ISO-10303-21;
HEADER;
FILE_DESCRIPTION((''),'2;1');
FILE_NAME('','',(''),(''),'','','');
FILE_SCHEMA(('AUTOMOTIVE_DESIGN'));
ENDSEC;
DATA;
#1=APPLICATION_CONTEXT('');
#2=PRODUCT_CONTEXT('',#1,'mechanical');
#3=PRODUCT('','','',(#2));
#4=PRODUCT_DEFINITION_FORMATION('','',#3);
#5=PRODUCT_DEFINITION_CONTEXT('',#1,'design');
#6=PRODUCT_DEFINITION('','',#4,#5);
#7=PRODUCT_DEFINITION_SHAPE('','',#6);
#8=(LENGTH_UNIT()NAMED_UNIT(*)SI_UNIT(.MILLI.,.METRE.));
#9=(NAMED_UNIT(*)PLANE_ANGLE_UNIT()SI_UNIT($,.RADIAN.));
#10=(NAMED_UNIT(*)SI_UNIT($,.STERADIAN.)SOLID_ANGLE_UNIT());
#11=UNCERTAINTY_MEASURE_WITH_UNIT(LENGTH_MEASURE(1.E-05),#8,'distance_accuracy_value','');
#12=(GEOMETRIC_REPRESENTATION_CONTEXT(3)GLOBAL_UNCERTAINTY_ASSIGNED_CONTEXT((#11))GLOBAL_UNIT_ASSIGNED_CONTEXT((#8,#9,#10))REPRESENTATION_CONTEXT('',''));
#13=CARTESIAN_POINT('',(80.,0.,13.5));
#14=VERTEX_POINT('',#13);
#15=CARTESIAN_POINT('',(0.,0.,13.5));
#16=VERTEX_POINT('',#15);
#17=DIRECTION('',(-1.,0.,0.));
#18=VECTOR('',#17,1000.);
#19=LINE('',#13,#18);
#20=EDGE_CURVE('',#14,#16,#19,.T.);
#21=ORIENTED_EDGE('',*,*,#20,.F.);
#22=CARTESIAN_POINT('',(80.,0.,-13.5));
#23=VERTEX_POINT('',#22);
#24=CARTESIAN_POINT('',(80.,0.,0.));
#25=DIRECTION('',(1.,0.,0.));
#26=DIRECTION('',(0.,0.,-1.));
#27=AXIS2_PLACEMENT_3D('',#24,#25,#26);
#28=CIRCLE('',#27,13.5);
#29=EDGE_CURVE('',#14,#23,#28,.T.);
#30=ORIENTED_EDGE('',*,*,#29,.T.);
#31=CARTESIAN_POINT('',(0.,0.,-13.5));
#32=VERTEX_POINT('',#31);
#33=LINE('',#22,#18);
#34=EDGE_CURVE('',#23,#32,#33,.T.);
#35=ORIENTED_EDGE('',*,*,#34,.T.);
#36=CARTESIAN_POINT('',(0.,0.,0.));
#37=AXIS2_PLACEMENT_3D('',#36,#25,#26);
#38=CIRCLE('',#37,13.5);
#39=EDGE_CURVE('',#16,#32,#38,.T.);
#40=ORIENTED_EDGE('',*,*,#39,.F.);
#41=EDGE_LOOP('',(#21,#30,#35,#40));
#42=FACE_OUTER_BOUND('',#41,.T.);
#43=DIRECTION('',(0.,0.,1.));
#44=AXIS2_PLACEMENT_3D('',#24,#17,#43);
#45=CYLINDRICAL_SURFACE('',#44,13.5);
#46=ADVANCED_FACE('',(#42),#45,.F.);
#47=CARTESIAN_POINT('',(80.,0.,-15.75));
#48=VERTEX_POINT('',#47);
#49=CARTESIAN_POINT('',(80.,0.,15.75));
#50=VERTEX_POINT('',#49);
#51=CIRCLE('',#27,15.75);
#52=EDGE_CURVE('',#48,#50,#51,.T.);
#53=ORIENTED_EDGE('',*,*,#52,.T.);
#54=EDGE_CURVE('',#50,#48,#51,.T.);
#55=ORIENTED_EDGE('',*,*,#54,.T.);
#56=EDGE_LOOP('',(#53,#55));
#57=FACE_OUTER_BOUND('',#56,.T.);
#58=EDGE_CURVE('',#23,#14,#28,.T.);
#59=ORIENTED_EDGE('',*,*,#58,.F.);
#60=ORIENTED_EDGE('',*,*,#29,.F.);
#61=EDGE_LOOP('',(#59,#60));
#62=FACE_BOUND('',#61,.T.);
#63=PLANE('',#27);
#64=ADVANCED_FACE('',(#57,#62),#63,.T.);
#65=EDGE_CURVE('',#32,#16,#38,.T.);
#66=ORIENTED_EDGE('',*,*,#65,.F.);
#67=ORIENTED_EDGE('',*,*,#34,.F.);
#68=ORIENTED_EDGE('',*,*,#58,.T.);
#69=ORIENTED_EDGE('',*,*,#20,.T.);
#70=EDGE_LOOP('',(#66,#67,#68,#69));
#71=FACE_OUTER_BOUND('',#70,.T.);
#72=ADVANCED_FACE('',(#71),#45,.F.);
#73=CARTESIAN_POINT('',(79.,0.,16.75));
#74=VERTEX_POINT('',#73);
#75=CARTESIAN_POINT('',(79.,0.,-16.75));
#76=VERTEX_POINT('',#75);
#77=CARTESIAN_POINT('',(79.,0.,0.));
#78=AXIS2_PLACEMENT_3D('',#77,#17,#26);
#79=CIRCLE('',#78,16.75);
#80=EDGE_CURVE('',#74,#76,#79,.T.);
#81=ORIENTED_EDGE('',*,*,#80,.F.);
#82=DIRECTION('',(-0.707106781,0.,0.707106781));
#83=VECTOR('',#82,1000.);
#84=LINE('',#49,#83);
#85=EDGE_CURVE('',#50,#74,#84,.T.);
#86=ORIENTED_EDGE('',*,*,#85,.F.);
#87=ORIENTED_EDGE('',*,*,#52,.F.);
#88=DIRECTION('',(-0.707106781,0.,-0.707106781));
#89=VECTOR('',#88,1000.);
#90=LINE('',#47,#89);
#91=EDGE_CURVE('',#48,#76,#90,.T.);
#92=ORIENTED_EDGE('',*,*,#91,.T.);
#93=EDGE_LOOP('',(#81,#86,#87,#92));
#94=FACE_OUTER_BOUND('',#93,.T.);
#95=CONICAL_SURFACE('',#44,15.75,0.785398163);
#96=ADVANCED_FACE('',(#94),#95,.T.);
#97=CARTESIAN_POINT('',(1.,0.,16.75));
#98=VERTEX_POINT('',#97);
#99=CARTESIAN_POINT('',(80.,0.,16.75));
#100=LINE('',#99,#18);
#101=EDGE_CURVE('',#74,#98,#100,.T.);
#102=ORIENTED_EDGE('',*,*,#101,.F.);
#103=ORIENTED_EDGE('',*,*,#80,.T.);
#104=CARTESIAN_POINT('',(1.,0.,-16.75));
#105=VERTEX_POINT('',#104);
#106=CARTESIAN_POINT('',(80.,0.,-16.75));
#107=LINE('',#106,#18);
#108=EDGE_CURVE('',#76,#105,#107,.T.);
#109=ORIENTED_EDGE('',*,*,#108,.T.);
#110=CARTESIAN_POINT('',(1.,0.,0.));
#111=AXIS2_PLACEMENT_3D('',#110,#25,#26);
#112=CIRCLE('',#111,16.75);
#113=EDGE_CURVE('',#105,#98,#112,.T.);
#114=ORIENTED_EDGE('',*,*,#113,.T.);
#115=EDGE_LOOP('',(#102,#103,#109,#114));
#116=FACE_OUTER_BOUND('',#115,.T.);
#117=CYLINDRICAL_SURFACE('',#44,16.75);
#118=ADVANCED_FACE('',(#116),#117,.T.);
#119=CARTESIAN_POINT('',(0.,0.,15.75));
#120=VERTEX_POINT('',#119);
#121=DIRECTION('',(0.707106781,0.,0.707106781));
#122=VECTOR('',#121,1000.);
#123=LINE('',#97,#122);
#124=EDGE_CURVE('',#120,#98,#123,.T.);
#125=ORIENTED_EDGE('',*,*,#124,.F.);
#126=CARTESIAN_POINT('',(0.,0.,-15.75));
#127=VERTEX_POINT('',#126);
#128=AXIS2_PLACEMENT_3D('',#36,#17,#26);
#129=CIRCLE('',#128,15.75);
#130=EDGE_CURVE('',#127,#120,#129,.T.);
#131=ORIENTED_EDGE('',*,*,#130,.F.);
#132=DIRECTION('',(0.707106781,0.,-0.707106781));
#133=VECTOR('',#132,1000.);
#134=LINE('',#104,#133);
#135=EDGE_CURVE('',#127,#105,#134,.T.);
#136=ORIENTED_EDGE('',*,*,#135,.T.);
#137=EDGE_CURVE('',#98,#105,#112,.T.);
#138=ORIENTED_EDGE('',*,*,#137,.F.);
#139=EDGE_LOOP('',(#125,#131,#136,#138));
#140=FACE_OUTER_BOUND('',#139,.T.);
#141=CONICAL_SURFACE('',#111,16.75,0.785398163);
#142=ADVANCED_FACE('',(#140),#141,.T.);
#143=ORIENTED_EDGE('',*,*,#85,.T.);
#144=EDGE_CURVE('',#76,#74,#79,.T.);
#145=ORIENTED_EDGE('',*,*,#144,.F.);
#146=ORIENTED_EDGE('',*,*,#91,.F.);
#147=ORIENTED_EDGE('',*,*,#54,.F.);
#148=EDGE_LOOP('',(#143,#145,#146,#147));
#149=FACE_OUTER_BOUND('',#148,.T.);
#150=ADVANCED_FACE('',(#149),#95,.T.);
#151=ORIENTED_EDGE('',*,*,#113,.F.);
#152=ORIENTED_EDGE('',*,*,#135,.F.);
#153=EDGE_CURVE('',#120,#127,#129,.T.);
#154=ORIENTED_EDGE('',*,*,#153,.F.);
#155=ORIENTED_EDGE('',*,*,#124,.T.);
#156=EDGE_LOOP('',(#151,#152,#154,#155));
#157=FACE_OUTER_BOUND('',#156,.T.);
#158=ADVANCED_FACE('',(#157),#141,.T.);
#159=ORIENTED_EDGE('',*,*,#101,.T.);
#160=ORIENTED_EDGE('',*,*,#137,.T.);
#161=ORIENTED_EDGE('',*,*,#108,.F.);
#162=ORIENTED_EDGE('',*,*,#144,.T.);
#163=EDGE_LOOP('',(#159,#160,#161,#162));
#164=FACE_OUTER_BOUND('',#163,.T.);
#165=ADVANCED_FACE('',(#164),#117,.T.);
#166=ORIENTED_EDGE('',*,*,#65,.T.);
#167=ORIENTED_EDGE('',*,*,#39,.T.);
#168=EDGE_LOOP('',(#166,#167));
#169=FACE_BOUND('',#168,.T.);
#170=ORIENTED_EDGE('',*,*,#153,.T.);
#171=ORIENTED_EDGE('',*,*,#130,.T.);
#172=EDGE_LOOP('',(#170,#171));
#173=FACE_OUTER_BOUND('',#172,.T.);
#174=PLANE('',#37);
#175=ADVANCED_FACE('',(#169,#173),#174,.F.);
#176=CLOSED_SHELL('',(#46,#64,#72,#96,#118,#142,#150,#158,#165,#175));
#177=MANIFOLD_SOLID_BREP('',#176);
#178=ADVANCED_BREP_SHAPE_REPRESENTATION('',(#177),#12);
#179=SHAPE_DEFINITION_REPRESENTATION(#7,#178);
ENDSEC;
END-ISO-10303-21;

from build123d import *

# Parameters (mm, degrees)
SKETCH_1_R      = 16.75
SKETCH_1_R_2    = 13.5
EXTRUDE_1_DEPTH = 80
CHAMFER_1_SIZE  = 1


with BuildPart() as part:
    # 草图1 → 拉伸-薄壁1 (new body)
    with BuildSketch(Plane(origin=(0, 0, 0), x_dir=(0, 0, -1), z_dir=(1, 0, 0))):
        Circle(SKETCH_1_R)
        Circle(SKETCH_1_R_2, mode=Mode.SUBTRACT)
    extrude(amount=EXTRUDE_1_DEPTH)

    # 倒角1
    chamfer_1_edges = [part.edges().sort_by_distance(p)[0] for p in [
        (0, 0, 16.75),
        (80, 0, 16.75),
    ]]
    chamfer(chamfer_1_edges, length=CHAMFER_1_SIZE)


solid = part.part
